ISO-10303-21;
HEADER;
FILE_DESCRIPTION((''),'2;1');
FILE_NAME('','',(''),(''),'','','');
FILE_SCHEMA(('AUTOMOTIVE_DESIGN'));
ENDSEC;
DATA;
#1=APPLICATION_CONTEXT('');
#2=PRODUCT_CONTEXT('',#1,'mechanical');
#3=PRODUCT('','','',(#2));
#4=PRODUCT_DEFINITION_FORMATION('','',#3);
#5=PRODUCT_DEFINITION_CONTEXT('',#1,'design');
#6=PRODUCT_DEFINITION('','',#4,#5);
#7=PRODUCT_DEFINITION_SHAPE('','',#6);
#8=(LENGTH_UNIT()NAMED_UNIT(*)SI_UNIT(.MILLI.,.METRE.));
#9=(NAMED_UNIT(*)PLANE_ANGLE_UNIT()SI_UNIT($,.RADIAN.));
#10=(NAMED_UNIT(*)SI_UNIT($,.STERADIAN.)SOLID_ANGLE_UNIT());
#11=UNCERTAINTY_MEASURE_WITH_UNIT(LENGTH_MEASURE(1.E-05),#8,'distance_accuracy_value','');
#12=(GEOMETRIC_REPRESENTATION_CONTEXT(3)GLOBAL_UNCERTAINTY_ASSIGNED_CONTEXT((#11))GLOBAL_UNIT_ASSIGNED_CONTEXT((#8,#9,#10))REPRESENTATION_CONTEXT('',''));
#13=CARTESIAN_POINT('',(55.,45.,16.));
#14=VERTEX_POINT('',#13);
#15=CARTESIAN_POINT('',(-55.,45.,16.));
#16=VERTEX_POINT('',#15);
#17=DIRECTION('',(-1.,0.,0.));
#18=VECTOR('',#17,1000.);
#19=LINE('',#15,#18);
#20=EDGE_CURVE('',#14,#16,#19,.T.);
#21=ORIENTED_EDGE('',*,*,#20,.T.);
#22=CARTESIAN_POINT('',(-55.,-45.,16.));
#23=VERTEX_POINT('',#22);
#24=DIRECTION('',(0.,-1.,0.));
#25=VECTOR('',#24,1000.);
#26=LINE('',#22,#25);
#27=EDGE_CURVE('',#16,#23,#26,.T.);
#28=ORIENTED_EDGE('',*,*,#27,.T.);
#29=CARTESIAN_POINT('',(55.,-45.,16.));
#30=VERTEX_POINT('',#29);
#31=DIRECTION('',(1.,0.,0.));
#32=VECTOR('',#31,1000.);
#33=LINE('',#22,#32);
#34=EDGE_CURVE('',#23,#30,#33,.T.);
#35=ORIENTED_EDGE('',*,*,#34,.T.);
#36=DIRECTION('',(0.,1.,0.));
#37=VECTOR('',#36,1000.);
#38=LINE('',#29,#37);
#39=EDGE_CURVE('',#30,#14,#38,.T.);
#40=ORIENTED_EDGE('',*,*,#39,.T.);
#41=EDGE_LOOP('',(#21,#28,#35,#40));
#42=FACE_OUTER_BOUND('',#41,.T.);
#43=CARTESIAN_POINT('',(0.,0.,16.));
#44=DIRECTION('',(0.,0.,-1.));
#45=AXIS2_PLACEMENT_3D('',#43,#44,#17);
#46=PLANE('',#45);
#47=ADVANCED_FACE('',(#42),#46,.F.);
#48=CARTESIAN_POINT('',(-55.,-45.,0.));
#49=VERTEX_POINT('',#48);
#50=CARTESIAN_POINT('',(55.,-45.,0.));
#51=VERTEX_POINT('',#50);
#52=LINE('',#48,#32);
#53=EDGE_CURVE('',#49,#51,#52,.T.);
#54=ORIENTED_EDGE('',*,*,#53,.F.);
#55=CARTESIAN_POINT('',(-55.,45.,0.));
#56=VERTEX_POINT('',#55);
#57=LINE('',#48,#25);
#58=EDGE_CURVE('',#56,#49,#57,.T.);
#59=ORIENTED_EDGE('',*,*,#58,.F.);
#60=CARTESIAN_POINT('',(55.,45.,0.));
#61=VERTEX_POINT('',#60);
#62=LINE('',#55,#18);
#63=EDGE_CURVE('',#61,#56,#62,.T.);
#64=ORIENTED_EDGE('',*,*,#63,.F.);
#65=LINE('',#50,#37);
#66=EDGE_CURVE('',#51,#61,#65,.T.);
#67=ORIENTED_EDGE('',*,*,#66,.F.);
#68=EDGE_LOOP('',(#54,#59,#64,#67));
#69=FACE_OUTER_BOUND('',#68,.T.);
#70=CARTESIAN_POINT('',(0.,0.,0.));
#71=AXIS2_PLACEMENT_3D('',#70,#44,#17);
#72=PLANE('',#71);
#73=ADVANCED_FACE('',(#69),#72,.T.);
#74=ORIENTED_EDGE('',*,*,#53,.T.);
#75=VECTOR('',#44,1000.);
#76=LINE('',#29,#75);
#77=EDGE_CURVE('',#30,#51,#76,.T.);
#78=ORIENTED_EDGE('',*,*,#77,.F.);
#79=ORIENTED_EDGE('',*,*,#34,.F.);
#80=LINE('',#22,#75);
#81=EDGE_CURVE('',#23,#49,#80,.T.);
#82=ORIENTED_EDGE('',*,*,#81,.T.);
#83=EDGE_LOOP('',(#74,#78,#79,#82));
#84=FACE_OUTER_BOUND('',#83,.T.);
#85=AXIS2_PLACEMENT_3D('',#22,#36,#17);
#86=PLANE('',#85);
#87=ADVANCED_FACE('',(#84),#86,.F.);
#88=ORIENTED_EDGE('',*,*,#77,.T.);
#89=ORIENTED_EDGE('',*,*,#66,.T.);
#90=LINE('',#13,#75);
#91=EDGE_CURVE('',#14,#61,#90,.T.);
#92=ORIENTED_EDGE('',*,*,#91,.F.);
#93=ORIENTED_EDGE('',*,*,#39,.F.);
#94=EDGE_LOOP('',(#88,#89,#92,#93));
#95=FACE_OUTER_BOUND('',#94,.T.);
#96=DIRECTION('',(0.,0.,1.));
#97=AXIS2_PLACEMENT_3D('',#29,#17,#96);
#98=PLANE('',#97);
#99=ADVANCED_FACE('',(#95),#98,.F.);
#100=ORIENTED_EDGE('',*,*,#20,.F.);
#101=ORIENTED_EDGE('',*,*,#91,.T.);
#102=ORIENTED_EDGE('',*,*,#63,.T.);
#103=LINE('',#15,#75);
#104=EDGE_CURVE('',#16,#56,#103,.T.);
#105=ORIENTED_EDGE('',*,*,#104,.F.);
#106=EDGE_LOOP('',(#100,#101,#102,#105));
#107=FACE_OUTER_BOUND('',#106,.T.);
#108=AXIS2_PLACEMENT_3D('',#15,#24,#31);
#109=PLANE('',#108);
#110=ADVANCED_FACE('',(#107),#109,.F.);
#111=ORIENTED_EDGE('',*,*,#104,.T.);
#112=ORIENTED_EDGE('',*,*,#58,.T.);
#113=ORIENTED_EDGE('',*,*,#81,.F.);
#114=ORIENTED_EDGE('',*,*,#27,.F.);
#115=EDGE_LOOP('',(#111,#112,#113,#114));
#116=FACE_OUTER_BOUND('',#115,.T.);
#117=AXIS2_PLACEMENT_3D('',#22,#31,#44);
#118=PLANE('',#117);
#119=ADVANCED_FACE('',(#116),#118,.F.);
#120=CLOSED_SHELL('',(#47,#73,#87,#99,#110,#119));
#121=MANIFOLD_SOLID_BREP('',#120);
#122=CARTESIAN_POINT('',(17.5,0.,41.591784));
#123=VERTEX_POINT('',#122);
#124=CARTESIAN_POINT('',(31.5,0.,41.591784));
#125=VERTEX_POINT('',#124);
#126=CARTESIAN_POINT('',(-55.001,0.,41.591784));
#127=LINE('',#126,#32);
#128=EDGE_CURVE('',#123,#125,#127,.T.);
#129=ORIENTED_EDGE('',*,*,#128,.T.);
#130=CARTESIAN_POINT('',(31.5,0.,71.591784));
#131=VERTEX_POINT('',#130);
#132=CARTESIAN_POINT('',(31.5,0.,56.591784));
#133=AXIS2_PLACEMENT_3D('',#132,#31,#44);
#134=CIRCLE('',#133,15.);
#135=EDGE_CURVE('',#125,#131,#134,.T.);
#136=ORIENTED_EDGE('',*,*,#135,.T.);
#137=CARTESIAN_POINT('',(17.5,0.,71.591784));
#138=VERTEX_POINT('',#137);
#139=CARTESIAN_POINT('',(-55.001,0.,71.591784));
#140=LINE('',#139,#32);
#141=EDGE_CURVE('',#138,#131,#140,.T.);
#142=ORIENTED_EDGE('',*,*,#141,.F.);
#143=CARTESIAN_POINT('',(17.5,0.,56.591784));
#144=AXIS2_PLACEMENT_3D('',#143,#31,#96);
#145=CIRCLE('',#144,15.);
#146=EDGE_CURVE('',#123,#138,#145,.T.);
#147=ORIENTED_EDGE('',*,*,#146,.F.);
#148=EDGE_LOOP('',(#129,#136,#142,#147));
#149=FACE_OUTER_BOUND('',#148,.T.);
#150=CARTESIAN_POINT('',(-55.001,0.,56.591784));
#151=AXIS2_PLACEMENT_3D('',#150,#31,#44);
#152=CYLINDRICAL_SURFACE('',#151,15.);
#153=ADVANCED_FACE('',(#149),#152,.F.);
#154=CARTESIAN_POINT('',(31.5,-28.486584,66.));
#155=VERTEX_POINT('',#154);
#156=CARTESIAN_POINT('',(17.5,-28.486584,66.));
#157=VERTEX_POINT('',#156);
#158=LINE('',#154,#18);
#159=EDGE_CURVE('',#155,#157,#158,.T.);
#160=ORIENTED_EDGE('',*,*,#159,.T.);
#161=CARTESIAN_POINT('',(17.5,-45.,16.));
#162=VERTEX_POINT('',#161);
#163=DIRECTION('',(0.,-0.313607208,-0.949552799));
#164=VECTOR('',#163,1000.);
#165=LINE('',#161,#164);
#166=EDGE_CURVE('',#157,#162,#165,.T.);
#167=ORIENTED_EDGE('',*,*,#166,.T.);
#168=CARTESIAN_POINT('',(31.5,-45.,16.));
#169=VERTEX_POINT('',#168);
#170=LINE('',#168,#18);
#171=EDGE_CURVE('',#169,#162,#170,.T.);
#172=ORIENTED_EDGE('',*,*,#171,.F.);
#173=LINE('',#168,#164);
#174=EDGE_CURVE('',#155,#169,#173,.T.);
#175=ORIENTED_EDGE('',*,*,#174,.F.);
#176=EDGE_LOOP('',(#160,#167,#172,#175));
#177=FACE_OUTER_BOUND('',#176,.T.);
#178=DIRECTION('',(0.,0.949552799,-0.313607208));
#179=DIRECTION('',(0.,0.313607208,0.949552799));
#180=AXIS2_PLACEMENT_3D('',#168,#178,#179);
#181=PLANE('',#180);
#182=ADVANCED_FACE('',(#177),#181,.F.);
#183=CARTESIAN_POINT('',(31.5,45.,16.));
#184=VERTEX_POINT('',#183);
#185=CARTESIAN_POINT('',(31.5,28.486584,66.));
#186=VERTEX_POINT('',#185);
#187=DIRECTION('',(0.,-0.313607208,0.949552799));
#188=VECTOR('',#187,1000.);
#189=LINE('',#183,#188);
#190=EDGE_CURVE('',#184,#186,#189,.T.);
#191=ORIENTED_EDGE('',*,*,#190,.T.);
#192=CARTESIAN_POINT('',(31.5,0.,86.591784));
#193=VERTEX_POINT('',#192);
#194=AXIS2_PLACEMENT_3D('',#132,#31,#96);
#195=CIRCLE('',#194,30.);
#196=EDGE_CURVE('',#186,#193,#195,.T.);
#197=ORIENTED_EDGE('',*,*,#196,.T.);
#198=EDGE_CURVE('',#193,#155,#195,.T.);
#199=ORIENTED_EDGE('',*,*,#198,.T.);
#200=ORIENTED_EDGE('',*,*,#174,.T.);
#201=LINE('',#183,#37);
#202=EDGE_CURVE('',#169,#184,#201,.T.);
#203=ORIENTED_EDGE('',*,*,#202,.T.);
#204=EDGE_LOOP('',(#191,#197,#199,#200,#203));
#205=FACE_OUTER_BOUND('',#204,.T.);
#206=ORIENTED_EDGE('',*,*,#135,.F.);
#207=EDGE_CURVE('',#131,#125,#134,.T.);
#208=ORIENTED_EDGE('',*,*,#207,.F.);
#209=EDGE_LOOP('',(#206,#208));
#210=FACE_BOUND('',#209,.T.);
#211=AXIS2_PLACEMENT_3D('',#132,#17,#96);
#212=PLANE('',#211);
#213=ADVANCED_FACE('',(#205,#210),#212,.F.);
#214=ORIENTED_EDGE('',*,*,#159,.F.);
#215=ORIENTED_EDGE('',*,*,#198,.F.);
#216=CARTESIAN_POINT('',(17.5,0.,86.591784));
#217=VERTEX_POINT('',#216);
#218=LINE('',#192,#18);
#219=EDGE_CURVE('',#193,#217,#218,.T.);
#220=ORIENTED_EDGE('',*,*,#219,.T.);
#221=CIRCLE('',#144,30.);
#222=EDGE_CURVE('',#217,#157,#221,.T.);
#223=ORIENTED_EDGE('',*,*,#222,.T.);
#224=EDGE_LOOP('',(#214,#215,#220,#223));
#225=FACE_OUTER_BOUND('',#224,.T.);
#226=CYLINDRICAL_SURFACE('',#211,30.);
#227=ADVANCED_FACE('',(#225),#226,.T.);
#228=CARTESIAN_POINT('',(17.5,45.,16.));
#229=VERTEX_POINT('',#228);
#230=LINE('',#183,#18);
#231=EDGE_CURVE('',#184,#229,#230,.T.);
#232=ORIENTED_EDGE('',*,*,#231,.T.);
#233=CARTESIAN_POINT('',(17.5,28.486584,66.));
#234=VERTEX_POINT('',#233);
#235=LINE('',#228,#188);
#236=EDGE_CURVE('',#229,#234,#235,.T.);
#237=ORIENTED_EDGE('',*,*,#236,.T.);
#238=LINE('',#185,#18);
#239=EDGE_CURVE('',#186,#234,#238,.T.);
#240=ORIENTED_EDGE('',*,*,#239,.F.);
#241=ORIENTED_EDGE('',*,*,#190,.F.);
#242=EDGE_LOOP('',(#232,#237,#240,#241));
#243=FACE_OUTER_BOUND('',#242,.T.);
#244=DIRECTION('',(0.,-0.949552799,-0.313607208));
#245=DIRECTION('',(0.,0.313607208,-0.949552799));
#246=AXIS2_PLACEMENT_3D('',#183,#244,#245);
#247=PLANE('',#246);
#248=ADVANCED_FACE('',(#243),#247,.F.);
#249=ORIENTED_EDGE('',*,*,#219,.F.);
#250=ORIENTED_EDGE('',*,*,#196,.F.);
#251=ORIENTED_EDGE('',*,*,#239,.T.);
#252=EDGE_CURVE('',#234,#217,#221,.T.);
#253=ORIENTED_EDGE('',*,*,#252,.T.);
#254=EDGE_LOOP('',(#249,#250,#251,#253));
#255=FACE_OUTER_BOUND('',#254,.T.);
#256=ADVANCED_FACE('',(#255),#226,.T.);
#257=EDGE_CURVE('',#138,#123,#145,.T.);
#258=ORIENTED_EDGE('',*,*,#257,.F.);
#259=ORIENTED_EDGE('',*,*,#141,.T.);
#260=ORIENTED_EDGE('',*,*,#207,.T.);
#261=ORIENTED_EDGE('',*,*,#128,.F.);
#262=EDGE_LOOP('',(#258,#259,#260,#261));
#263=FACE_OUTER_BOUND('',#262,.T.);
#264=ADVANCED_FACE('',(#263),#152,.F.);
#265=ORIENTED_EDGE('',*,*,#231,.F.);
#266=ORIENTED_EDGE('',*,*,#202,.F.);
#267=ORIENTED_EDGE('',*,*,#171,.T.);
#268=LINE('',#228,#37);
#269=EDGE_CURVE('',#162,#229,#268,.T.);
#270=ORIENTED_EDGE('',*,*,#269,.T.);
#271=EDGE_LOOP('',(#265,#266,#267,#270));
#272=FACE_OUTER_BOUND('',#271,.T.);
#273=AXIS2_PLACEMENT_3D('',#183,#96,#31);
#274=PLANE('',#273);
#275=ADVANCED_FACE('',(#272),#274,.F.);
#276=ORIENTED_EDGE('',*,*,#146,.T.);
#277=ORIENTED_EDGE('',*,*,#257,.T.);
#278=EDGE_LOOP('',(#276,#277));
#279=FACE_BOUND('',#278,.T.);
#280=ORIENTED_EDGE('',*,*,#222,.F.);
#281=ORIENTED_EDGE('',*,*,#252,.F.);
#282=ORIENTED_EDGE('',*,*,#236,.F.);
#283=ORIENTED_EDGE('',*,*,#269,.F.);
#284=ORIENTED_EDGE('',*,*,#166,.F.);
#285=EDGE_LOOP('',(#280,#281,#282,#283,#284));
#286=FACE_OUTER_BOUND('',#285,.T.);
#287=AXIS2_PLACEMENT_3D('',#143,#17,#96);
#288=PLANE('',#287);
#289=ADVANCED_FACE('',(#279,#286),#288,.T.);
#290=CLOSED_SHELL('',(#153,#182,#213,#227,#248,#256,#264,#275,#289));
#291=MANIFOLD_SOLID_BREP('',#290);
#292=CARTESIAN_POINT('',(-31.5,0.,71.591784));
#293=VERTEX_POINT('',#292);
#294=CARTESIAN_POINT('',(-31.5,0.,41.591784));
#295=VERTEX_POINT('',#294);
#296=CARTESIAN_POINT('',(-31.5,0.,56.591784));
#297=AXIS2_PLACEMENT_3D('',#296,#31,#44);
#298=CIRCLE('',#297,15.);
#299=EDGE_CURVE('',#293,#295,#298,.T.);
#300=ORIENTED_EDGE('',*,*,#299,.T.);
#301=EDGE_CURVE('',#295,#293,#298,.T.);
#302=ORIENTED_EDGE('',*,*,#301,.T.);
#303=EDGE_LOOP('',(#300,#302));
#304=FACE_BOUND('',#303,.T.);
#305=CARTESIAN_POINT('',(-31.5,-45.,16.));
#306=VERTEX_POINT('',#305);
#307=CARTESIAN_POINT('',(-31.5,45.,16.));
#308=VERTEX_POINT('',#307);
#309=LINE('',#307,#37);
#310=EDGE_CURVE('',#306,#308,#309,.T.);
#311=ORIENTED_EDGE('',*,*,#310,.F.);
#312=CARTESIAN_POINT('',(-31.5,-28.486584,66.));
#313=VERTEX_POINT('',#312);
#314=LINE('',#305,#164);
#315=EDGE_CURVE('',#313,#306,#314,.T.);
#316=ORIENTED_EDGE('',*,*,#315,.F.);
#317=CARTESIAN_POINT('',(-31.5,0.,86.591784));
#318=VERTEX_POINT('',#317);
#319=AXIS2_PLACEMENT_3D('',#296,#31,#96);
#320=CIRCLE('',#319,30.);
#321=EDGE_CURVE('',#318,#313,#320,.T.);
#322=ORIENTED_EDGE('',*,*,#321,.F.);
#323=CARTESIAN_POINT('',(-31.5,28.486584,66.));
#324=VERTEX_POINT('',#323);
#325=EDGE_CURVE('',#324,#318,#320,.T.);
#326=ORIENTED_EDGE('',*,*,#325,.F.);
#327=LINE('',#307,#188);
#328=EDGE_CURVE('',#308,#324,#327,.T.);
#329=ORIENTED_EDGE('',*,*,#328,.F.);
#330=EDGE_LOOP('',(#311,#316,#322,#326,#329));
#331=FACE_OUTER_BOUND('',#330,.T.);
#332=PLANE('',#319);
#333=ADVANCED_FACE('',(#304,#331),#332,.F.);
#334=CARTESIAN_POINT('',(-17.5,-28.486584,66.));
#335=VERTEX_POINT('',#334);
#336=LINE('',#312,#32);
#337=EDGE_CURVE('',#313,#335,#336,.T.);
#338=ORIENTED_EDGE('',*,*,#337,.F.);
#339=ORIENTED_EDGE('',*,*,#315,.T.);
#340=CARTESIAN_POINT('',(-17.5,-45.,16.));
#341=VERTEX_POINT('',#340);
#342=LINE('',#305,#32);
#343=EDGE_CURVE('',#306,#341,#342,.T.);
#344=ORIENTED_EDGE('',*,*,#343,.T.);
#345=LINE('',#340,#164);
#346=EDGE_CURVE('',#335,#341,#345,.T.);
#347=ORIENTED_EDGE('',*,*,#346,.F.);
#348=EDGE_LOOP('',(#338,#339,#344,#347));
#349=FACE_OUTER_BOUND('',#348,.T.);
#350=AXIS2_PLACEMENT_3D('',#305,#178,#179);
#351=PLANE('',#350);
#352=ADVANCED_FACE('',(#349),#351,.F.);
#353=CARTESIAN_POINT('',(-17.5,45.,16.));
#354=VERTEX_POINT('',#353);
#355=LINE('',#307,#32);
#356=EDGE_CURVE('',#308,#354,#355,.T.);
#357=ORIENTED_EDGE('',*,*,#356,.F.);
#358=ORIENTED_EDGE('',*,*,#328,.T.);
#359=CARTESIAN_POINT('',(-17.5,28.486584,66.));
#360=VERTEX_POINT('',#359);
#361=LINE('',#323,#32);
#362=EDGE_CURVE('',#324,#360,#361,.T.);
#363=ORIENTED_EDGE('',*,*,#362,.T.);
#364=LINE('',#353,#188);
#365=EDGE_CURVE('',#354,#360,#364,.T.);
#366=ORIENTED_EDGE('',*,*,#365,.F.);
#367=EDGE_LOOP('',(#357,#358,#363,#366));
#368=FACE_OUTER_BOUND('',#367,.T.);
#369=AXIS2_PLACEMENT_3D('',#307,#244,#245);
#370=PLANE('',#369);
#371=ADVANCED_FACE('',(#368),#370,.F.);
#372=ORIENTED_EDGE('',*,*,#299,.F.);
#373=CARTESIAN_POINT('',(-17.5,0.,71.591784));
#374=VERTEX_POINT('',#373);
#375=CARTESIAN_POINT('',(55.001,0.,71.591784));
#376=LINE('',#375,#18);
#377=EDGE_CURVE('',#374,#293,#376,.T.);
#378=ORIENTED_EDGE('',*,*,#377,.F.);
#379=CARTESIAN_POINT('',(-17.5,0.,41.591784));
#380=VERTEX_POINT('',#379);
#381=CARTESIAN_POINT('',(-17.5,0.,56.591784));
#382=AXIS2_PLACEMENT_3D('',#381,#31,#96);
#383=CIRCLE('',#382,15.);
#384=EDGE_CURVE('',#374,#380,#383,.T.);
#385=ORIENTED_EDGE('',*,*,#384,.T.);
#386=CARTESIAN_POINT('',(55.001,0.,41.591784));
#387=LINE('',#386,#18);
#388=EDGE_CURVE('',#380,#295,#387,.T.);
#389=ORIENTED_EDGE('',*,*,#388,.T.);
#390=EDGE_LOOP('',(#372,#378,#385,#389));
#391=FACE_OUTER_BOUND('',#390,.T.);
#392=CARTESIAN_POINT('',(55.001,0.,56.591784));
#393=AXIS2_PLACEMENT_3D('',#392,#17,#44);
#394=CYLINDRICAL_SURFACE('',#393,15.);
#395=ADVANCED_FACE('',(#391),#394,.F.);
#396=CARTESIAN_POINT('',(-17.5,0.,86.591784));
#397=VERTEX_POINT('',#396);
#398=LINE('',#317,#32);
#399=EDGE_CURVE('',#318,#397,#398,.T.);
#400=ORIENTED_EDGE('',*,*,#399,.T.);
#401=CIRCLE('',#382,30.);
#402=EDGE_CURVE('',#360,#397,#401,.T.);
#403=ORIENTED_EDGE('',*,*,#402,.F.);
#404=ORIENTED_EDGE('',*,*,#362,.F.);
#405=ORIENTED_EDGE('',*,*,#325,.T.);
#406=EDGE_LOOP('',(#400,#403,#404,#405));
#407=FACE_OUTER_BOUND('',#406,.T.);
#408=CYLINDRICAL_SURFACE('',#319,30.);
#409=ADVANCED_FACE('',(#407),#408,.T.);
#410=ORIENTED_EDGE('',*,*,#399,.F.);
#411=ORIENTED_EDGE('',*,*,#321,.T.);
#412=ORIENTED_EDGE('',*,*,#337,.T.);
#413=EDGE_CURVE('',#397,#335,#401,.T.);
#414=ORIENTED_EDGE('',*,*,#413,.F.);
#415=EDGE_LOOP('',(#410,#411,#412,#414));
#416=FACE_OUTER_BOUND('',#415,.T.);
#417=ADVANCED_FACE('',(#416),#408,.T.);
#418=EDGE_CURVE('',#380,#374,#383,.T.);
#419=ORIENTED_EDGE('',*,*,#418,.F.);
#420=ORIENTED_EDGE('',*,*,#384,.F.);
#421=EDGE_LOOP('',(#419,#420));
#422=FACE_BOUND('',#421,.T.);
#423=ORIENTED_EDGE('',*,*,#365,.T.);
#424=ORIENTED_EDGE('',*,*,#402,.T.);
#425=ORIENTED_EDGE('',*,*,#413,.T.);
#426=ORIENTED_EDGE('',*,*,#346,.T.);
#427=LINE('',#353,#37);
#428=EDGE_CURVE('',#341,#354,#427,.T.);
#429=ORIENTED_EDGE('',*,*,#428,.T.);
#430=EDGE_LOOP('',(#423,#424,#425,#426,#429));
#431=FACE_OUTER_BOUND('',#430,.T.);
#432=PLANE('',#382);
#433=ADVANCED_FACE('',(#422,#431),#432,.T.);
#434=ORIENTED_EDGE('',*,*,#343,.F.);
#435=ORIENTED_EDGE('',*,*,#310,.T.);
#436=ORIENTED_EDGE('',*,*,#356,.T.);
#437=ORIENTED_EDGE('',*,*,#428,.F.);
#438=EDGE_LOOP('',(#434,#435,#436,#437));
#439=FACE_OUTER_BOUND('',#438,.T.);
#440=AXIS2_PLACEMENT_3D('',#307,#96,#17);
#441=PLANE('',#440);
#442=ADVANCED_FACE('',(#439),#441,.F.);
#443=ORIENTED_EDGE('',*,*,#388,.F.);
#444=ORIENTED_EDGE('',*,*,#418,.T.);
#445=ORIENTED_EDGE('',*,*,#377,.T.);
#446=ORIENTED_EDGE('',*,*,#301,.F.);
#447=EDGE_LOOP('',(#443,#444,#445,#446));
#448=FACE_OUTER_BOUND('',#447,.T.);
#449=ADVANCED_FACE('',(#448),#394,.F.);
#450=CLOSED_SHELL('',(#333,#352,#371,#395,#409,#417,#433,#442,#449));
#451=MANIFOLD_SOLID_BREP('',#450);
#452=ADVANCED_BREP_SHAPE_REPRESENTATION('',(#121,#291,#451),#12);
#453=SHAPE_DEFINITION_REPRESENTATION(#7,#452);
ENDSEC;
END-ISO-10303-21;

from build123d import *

# Parameters (mm, degrees)
SKETCH_1_W          = 110
SKETCH_1_H          = 90
EXTRUDE_1_DEPTH     = 16
EXTRUDE_2_DEPTH     = 14
SKETCH_3_R          = 15
CUT_EXTRUDE_1_DEPTH = 14


with BuildPart() as part:
    # 草图1 → 凸台-拉伸1 (new body)
    with BuildSketch(Plane.XY):
        Rectangle(SKETCH_1_W, SKETCH_1_H)
    extrude(amount=EXTRUDE_1_DEPTH)


with BuildPart() as body_2:
    # 草图2 → 凸台-拉伸2 (new body)
    with BuildSketch(Plane(origin=(17.5, 0, 0), x_dir=(0, 0, -1), z_dir=(1, 0, 0))):
        with BuildLine():
            Line((-16, 45), (-66, 28.486583985))
            ThreePointArc((-66, 28.486583985), (-86.591783756, 0), (-66, -28.486583985))
            Line((-66, -28.486583985), (-16, -45))
            Line((-16, -45), (-16, 45))
        make_face()
    extrude(amount=EXTRUDE_2_DEPTH)

    # 草图3 → 切除-拉伸1 (cut)
    with BuildSketch(Plane(origin=(31.5, 0, 0), x_dir=(0, 0, -1), z_dir=(1, 0, 0))):
        with Locations((-56.591783756, 0)):
            Circle(SKETCH_3_R)
    extrude(amount=-CUT_EXTRUDE_1_DEPTH, mode=Mode.SUBTRACT)


with BuildPart() as body_3:
    # 镜向1: mirrored copy
    add(body_2.part.mirror(Plane(origin=(0, 0, 0), x_dir=(0, 0, 1), z_dir=(1, 0, 0))))


solid = Compound([part.part, body_2.part, body_3.part])
